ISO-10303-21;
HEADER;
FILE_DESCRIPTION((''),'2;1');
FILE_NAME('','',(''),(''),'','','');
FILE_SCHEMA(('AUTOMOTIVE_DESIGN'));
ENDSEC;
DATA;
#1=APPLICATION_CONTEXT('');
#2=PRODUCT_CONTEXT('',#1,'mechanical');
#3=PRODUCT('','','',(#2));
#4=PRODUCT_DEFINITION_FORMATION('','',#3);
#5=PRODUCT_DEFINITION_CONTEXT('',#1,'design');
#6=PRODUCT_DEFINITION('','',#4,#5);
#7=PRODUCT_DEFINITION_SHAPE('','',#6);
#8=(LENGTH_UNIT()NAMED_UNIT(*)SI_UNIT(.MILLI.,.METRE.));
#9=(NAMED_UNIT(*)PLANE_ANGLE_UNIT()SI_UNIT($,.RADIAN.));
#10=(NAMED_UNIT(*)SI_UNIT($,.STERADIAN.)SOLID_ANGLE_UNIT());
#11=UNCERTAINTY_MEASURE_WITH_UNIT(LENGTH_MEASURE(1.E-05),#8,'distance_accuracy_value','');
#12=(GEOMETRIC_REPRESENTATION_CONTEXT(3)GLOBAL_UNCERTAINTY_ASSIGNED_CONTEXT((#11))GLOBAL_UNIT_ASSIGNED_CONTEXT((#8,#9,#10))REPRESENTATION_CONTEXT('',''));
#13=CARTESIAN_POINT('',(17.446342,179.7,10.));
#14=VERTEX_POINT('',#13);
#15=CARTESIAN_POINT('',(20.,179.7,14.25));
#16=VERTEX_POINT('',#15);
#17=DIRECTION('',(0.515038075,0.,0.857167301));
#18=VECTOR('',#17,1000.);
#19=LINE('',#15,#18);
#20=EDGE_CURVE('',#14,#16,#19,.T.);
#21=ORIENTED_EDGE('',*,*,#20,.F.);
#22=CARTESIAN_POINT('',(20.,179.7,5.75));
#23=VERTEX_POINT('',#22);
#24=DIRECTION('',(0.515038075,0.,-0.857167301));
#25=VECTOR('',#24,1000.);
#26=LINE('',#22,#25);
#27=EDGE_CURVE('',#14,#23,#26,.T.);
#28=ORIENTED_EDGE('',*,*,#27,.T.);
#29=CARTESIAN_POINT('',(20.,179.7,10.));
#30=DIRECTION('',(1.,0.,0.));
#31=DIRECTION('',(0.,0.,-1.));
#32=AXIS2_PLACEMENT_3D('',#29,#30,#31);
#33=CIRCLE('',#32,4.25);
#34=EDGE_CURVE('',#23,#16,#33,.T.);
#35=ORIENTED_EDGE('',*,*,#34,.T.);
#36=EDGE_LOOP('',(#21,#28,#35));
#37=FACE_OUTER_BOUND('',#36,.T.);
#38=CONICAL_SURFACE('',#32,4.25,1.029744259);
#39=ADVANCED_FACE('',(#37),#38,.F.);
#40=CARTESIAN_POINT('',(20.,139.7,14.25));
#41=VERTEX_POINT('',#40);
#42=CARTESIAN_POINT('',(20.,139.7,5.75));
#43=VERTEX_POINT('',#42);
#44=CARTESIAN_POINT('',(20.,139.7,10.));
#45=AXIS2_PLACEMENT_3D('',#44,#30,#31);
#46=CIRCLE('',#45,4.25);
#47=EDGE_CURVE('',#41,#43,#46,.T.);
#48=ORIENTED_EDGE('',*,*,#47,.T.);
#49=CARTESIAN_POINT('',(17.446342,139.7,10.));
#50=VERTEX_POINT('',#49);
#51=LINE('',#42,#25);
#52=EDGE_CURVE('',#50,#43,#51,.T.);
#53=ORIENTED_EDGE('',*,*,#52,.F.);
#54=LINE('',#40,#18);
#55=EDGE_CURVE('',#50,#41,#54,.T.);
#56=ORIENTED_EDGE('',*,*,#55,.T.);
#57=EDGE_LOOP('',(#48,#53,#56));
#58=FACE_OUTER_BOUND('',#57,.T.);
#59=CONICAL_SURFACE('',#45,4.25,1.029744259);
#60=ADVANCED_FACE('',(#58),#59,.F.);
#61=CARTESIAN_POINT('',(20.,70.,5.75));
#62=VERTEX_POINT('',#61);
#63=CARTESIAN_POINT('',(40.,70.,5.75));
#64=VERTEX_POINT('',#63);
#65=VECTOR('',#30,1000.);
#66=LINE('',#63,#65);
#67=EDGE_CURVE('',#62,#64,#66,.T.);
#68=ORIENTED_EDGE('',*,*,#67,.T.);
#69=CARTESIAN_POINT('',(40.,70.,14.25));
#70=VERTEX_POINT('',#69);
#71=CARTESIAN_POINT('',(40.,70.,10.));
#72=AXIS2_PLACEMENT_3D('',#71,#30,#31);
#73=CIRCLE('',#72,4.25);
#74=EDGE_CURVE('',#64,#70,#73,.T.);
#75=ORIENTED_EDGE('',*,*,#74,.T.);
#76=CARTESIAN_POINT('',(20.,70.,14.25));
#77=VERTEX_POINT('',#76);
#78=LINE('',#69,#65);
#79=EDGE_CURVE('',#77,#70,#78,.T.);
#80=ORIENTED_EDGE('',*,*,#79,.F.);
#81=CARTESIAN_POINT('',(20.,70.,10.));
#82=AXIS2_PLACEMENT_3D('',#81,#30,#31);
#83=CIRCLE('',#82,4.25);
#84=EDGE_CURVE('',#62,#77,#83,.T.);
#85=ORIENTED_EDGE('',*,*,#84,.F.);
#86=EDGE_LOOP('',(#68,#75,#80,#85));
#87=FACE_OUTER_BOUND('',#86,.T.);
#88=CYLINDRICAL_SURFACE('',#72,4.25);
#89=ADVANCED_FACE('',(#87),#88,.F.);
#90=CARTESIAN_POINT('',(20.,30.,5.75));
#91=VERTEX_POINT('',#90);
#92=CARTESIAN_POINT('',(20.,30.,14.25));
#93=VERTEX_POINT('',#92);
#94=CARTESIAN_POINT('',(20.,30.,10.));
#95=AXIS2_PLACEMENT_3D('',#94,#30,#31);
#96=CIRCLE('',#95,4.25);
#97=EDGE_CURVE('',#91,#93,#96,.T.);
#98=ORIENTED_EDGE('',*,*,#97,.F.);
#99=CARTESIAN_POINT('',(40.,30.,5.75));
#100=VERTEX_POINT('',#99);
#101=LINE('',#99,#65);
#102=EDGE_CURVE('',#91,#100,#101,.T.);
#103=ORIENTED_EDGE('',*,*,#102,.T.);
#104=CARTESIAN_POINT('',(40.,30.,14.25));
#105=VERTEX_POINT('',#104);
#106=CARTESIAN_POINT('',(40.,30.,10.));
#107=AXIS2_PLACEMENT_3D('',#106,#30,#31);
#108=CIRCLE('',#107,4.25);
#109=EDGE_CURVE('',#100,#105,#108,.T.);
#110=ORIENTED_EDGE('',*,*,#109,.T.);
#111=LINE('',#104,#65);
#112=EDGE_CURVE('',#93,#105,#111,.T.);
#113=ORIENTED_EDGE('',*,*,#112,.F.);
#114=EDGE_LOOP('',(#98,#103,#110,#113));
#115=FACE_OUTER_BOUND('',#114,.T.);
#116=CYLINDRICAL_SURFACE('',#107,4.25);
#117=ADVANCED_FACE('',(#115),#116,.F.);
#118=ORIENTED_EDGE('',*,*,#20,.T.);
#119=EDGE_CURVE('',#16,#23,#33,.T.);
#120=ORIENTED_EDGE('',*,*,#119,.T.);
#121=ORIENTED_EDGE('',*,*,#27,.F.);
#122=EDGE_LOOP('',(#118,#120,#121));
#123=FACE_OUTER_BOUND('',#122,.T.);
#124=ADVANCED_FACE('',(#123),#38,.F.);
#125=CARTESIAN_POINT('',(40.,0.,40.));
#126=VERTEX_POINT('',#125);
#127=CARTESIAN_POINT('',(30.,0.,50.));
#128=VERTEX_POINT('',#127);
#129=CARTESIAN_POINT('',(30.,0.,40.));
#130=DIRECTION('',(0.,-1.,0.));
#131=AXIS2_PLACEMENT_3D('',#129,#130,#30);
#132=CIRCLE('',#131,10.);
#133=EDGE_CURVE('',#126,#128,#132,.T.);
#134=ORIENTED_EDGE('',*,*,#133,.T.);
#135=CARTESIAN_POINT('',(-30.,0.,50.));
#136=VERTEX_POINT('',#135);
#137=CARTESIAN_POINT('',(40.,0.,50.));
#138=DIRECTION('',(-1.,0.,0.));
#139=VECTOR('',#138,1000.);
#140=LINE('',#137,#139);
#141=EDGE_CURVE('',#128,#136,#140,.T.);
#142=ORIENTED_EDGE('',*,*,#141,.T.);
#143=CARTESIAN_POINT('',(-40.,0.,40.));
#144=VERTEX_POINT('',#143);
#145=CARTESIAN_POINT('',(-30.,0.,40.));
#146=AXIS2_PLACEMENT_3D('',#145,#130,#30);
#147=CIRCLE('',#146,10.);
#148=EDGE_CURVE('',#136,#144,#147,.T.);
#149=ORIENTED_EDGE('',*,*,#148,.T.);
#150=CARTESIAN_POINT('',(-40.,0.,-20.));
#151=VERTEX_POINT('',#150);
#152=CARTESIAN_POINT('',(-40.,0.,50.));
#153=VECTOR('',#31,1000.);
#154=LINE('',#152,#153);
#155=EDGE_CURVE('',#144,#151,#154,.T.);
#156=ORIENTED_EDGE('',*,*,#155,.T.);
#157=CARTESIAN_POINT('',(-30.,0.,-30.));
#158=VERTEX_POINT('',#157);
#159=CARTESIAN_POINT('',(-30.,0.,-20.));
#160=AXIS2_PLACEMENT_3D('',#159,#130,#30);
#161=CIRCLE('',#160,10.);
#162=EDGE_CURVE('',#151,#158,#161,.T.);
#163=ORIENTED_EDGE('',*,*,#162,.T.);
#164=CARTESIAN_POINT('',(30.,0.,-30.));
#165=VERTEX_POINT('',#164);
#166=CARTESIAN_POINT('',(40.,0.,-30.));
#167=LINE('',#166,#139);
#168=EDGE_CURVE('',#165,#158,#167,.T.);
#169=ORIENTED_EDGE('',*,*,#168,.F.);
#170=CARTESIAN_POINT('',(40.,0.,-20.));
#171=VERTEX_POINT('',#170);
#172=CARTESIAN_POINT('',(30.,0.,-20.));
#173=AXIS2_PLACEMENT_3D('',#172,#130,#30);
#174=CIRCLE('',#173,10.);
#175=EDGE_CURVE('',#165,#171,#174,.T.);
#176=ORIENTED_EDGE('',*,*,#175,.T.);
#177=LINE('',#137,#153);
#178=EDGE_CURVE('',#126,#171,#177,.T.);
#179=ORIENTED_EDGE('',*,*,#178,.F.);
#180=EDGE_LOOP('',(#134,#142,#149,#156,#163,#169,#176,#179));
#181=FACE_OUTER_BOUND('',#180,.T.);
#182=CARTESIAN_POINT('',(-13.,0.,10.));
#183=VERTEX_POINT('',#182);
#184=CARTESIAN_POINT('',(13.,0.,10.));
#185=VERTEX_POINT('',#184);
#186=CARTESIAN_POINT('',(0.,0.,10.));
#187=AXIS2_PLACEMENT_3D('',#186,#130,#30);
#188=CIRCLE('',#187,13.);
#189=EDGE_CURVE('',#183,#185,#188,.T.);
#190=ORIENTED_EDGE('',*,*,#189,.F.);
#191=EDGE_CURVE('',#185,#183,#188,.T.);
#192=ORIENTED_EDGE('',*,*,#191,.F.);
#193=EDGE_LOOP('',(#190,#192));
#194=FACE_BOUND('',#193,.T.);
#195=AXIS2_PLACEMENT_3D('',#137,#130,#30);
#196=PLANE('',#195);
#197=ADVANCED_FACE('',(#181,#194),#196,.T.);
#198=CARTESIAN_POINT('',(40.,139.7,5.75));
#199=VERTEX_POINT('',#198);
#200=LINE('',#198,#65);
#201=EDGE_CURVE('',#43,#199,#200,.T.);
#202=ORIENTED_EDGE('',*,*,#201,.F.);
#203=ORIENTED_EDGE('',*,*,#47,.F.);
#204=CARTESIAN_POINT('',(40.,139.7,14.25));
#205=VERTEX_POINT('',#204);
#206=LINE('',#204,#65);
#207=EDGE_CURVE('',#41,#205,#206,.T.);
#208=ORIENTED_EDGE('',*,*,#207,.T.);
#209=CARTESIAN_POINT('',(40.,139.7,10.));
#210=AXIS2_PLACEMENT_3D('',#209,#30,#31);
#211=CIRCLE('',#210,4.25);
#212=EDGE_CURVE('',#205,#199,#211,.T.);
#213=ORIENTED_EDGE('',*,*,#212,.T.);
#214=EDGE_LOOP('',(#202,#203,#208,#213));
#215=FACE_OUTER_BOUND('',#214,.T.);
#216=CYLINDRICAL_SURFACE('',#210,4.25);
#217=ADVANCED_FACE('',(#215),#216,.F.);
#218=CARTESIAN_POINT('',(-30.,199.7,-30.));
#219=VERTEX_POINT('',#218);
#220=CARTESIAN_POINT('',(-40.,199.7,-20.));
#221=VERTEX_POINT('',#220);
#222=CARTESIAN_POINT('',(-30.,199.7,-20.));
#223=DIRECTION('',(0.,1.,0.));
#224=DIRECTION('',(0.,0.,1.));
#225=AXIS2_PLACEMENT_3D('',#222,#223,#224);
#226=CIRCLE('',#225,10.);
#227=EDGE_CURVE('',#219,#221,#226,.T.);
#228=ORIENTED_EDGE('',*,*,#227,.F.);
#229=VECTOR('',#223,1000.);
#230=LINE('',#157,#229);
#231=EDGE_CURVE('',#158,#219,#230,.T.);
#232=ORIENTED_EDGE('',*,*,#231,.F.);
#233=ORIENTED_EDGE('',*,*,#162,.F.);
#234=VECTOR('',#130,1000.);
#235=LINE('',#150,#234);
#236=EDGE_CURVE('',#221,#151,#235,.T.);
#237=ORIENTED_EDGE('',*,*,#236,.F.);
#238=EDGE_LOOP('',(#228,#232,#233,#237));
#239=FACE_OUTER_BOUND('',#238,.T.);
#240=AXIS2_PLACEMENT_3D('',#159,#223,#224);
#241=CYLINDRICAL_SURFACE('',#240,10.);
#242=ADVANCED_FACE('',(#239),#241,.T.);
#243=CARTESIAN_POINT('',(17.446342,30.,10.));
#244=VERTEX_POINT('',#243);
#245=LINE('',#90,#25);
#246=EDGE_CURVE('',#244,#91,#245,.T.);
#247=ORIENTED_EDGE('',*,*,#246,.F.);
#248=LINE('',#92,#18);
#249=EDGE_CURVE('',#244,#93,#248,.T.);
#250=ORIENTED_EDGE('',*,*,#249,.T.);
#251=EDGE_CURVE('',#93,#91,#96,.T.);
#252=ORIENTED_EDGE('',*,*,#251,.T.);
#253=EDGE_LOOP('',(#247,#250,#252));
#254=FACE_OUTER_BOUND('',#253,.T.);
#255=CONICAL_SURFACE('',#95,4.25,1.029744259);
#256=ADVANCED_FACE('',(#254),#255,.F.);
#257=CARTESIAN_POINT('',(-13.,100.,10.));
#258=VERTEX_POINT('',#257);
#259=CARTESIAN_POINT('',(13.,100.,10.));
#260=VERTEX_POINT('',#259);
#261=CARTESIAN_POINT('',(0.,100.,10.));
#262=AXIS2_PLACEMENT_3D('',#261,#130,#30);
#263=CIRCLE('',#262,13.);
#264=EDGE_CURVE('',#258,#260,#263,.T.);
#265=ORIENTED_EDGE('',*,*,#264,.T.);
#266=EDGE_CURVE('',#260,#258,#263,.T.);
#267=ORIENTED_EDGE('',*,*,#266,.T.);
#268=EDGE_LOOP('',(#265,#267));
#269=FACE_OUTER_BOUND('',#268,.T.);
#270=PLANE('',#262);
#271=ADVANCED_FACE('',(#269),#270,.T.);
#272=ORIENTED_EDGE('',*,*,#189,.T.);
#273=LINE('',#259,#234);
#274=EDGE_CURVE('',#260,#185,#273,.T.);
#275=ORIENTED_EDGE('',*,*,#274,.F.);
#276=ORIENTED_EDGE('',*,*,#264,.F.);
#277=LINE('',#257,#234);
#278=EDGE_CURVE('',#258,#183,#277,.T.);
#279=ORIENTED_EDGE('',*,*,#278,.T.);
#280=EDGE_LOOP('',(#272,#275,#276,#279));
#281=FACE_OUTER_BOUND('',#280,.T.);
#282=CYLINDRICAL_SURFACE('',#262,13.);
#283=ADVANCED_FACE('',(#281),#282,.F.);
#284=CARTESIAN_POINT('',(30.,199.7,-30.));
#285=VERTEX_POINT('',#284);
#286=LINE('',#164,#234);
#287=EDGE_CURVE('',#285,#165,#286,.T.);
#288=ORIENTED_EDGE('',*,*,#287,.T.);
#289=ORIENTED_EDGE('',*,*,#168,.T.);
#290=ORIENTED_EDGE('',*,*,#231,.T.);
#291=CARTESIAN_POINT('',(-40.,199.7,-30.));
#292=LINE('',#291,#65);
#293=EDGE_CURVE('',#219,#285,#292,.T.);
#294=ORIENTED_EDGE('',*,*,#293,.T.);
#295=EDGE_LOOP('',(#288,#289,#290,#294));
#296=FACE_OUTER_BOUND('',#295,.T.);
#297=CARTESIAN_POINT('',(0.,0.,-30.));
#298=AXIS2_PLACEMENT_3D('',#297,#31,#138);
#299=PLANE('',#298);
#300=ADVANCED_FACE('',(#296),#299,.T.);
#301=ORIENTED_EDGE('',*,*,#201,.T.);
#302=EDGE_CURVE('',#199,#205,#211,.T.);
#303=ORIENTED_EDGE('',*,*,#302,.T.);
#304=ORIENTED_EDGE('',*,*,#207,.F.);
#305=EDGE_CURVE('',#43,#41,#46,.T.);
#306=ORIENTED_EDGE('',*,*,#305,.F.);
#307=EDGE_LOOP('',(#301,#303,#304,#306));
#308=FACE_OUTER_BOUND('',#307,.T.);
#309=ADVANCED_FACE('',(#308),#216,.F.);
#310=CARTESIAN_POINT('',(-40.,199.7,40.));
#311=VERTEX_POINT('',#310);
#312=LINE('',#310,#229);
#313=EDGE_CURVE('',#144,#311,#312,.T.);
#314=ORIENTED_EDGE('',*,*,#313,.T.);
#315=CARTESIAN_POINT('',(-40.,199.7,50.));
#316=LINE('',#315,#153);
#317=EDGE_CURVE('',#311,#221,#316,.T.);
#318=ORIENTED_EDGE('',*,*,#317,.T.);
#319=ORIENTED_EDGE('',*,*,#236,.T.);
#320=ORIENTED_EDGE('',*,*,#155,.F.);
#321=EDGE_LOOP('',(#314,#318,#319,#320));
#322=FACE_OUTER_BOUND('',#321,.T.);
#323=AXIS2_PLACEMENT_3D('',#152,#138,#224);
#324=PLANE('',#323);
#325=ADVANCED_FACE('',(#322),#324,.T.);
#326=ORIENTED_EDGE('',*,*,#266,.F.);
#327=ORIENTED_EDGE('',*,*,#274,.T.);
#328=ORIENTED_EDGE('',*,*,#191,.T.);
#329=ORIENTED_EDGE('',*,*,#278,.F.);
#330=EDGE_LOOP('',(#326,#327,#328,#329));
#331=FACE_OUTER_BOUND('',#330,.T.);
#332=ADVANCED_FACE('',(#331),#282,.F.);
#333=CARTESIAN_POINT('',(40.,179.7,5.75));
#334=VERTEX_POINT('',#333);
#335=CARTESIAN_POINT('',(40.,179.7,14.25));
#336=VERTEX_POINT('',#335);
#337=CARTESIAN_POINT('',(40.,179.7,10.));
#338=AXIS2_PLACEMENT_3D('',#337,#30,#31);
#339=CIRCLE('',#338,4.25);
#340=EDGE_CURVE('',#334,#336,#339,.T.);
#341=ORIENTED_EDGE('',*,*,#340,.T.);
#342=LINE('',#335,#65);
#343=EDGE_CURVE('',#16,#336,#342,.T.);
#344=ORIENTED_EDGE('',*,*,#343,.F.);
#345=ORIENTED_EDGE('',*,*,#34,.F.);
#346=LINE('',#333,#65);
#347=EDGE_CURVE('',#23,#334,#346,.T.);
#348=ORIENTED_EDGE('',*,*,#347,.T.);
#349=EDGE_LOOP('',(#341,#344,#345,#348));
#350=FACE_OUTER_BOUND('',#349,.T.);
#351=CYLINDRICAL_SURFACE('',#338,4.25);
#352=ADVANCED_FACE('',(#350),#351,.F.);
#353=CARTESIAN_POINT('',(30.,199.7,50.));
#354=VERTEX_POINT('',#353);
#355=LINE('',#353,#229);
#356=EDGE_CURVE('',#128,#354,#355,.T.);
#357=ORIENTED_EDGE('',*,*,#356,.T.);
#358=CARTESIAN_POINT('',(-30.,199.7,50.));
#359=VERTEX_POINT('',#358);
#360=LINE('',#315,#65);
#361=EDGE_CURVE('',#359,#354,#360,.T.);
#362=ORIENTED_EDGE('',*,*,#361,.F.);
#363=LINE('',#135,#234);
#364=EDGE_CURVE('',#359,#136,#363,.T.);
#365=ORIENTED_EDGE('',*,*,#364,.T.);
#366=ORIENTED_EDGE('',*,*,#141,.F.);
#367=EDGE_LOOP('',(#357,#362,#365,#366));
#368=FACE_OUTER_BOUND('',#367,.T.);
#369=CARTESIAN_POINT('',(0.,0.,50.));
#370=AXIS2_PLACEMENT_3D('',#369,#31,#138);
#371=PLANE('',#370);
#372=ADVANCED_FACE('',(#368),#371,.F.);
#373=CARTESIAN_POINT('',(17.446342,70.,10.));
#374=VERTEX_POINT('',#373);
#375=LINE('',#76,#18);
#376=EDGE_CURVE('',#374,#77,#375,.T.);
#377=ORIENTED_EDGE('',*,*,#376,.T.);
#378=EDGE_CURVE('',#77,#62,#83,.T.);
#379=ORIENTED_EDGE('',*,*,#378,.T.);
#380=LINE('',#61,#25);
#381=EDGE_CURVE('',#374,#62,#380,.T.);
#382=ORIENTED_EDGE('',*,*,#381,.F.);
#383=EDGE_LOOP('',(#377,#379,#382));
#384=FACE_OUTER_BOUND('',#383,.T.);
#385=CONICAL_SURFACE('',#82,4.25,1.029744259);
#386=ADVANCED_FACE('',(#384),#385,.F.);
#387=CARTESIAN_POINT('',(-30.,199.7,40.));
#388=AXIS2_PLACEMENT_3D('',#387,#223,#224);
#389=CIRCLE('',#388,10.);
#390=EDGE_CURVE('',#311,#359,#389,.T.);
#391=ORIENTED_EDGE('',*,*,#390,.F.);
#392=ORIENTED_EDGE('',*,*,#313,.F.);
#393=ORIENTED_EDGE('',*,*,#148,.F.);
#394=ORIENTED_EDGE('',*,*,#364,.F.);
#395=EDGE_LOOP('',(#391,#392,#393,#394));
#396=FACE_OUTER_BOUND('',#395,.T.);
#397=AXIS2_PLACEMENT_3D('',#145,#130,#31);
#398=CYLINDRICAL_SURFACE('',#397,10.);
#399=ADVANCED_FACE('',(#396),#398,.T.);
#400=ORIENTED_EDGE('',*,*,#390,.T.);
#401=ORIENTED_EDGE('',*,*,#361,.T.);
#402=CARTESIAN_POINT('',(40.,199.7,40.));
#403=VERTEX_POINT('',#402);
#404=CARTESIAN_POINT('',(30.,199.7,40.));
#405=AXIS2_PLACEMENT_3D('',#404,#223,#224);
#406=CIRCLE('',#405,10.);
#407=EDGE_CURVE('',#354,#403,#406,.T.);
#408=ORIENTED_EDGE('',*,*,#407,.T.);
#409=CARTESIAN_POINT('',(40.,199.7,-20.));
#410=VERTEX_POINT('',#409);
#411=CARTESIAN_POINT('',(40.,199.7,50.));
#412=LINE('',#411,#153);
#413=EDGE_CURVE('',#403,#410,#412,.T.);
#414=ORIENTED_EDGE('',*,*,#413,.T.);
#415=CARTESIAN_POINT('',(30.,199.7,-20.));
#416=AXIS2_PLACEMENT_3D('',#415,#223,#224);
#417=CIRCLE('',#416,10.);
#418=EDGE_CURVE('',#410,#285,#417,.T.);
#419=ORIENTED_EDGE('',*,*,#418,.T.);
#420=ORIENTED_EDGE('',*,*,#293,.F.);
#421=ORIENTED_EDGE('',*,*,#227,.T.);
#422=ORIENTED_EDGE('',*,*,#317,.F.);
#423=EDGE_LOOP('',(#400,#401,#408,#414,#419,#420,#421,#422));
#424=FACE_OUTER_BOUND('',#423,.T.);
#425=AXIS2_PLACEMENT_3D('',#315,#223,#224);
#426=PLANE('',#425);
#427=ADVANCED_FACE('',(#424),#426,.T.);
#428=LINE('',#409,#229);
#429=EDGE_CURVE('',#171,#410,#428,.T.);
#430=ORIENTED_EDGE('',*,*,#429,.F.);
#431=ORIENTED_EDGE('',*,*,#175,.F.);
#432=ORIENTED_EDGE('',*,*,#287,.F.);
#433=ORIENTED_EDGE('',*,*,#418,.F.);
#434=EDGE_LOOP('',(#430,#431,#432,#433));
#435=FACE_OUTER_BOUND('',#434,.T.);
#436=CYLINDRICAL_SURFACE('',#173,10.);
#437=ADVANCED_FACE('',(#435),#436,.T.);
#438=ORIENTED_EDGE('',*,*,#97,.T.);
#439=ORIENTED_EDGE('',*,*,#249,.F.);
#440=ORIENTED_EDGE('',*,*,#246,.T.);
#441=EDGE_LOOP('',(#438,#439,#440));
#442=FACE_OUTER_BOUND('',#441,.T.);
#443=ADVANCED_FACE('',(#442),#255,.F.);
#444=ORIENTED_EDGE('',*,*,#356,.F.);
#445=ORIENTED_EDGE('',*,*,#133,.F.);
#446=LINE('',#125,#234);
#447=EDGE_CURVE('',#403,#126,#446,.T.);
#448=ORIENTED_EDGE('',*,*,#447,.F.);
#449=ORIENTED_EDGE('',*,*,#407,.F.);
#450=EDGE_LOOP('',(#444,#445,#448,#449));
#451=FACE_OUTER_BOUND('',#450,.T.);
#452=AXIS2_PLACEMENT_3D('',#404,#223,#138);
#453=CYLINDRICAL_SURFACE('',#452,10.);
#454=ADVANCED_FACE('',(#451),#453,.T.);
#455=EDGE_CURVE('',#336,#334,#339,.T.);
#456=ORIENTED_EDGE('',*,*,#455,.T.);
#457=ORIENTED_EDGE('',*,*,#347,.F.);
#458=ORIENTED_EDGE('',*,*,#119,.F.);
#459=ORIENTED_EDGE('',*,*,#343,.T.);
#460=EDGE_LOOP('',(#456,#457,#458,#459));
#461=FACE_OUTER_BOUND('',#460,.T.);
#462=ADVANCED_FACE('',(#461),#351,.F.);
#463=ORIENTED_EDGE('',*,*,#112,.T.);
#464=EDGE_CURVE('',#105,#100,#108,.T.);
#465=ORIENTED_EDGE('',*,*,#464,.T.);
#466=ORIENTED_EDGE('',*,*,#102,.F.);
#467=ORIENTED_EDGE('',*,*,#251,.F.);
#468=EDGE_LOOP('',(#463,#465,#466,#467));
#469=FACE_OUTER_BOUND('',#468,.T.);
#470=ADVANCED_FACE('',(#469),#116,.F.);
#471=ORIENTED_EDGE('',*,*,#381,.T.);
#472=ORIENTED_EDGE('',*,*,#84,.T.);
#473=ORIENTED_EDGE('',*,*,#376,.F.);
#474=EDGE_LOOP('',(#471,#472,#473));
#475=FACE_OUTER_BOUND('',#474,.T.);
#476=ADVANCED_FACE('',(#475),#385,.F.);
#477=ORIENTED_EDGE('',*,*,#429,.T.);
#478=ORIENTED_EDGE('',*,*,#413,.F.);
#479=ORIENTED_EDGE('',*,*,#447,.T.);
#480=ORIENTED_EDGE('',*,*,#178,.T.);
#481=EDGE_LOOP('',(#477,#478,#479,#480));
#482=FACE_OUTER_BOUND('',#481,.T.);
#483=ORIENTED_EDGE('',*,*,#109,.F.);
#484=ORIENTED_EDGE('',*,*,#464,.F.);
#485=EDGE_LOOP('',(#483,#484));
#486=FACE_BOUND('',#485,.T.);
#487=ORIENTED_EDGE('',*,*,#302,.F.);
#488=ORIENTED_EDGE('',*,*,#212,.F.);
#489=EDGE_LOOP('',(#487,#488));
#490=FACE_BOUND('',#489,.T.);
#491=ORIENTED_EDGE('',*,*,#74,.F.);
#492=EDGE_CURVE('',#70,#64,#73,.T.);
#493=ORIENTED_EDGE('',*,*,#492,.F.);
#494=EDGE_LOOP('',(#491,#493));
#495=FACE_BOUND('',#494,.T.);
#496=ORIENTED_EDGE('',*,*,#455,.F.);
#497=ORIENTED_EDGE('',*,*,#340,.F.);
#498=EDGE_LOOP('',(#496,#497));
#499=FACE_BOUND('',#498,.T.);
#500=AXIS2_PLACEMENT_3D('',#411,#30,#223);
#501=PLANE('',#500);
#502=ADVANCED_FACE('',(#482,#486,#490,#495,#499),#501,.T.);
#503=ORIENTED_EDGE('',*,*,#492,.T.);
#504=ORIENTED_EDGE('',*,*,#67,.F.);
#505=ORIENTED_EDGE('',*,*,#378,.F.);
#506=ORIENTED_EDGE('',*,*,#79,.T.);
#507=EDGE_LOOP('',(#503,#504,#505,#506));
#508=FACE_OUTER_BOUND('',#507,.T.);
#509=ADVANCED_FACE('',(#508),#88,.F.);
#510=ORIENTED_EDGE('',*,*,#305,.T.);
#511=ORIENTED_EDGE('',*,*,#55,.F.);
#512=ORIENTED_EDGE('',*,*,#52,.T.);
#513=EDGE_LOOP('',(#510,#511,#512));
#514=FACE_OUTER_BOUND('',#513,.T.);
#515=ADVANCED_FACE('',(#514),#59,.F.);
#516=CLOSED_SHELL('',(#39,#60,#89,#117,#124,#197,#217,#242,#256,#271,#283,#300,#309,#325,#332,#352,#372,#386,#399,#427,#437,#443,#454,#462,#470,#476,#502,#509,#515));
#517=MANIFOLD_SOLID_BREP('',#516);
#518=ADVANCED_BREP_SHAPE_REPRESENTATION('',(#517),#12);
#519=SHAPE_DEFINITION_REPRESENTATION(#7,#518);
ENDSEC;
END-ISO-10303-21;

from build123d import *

# Parameters (mm, degrees)
SKETCH1_W                      = 80
SKETCH1_H                      = 199.7
BOSS_EXTRUDE1_DEPTH            = 80
F_8_5_8_5_DIAMETER_HOLE1_D     = 8.5
F_8_5_8_5_DIAMETER_HOLE1_DEPTH = 20
F_8_5_8_5_DIAMETER_HOLE1_TIP   = 2.553657631
FILLET2_R                      = 10
SKETCH5_R                      = 13
CUT_EXTRUDE1_DEPTH             = 100
F_8_5_8_5_DIAMETER_HOLE2_D     = 8.5
F_8_5_8_5_DIAMETER_HOLE2_DEPTH = 20
F_8_5_8_5_DIAMETER_HOLE2_TIP   = 2.553657631


with BuildPart() as part:
    # Sketch1 → Boss-Extrude1 (new body)
    with BuildSketch(Plane(origin=(0, 0, -30), x_dir=(-1, 0, 0), z_dir=(0, 0, -1))):
        with Locations((0, 99.85)):
            Rectangle(SKETCH1_W, SKETCH1_H)
    extrude(amount=-BOSS_EXTRUDE1_DEPTH)

    # Ø8.5 (8.5) Diameter Hole1
    with Locations(Plane(origin=(40, 0, 0), x_dir=(0, 0, -1), z_dir=(1, 0, 0))):
        with Locations((-10, 30), (-10, 179.7), (-10, 70)):
            Hole(F_8_5_8_5_DIAMETER_HOLE1_D / 2, depth=F_8_5_8_5_DIAMETER_HOLE1_DEPTH)
            with Locations((0, 0, -(F_8_5_8_5_DIAMETER_HOLE1_DEPTH + F_8_5_8_5_DIAMETER_HOLE1_TIP / 2))):  # 118° drill point
                Cone(0, F_8_5_8_5_DIAMETER_HOLE1_D / 2, F_8_5_8_5_DIAMETER_HOLE1_TIP, mode=Mode.SUBTRACT)

    # Fillet2
    fillet2_edges = [part.edges().sort_by_distance(p)[0] for p in [
        (-40, 99.85, 50),
        (40, 99.85, 50),
        (-40, 99.85, -30),
        (40, 99.85, -30),
    ]]
    fillet(fillet2_edges, radius=FILLET2_R)

    # Sketch5 → Cut-Extrude1 (cut)
    with BuildSketch(Plane.XZ):
        with Locations((0, 10)):
            Circle(SKETCH5_R)
    extrude(amount=-CUT_EXTRUDE1_DEPTH, mode=Mode.SUBTRACT)

    # Ø8.5 (8.5) Diameter Hole2
    with Locations(Plane(origin=(40, 0, 0), x_dir=(0, 0, -1), z_dir=(1, 0, 0))):
        with Locations((-10, 139.7)):
            Hole(F_8_5_8_5_DIAMETER_HOLE2_D / 2, depth=F_8_5_8_5_DIAMETER_HOLE2_DEPTH)
            with Locations((0, 0, -(F_8_5_8_5_DIAMETER_HOLE2_DEPTH + F_8_5_8_5_DIAMETER_HOLE2_TIP / 2))):  # 118° drill point
                Cone(0, F_8_5_8_5_DIAMETER_HOLE2_D / 2, F_8_5_8_5_DIAMETER_HOLE2_TIP, mode=Mode.SUBTRACT)


solid = part.part
